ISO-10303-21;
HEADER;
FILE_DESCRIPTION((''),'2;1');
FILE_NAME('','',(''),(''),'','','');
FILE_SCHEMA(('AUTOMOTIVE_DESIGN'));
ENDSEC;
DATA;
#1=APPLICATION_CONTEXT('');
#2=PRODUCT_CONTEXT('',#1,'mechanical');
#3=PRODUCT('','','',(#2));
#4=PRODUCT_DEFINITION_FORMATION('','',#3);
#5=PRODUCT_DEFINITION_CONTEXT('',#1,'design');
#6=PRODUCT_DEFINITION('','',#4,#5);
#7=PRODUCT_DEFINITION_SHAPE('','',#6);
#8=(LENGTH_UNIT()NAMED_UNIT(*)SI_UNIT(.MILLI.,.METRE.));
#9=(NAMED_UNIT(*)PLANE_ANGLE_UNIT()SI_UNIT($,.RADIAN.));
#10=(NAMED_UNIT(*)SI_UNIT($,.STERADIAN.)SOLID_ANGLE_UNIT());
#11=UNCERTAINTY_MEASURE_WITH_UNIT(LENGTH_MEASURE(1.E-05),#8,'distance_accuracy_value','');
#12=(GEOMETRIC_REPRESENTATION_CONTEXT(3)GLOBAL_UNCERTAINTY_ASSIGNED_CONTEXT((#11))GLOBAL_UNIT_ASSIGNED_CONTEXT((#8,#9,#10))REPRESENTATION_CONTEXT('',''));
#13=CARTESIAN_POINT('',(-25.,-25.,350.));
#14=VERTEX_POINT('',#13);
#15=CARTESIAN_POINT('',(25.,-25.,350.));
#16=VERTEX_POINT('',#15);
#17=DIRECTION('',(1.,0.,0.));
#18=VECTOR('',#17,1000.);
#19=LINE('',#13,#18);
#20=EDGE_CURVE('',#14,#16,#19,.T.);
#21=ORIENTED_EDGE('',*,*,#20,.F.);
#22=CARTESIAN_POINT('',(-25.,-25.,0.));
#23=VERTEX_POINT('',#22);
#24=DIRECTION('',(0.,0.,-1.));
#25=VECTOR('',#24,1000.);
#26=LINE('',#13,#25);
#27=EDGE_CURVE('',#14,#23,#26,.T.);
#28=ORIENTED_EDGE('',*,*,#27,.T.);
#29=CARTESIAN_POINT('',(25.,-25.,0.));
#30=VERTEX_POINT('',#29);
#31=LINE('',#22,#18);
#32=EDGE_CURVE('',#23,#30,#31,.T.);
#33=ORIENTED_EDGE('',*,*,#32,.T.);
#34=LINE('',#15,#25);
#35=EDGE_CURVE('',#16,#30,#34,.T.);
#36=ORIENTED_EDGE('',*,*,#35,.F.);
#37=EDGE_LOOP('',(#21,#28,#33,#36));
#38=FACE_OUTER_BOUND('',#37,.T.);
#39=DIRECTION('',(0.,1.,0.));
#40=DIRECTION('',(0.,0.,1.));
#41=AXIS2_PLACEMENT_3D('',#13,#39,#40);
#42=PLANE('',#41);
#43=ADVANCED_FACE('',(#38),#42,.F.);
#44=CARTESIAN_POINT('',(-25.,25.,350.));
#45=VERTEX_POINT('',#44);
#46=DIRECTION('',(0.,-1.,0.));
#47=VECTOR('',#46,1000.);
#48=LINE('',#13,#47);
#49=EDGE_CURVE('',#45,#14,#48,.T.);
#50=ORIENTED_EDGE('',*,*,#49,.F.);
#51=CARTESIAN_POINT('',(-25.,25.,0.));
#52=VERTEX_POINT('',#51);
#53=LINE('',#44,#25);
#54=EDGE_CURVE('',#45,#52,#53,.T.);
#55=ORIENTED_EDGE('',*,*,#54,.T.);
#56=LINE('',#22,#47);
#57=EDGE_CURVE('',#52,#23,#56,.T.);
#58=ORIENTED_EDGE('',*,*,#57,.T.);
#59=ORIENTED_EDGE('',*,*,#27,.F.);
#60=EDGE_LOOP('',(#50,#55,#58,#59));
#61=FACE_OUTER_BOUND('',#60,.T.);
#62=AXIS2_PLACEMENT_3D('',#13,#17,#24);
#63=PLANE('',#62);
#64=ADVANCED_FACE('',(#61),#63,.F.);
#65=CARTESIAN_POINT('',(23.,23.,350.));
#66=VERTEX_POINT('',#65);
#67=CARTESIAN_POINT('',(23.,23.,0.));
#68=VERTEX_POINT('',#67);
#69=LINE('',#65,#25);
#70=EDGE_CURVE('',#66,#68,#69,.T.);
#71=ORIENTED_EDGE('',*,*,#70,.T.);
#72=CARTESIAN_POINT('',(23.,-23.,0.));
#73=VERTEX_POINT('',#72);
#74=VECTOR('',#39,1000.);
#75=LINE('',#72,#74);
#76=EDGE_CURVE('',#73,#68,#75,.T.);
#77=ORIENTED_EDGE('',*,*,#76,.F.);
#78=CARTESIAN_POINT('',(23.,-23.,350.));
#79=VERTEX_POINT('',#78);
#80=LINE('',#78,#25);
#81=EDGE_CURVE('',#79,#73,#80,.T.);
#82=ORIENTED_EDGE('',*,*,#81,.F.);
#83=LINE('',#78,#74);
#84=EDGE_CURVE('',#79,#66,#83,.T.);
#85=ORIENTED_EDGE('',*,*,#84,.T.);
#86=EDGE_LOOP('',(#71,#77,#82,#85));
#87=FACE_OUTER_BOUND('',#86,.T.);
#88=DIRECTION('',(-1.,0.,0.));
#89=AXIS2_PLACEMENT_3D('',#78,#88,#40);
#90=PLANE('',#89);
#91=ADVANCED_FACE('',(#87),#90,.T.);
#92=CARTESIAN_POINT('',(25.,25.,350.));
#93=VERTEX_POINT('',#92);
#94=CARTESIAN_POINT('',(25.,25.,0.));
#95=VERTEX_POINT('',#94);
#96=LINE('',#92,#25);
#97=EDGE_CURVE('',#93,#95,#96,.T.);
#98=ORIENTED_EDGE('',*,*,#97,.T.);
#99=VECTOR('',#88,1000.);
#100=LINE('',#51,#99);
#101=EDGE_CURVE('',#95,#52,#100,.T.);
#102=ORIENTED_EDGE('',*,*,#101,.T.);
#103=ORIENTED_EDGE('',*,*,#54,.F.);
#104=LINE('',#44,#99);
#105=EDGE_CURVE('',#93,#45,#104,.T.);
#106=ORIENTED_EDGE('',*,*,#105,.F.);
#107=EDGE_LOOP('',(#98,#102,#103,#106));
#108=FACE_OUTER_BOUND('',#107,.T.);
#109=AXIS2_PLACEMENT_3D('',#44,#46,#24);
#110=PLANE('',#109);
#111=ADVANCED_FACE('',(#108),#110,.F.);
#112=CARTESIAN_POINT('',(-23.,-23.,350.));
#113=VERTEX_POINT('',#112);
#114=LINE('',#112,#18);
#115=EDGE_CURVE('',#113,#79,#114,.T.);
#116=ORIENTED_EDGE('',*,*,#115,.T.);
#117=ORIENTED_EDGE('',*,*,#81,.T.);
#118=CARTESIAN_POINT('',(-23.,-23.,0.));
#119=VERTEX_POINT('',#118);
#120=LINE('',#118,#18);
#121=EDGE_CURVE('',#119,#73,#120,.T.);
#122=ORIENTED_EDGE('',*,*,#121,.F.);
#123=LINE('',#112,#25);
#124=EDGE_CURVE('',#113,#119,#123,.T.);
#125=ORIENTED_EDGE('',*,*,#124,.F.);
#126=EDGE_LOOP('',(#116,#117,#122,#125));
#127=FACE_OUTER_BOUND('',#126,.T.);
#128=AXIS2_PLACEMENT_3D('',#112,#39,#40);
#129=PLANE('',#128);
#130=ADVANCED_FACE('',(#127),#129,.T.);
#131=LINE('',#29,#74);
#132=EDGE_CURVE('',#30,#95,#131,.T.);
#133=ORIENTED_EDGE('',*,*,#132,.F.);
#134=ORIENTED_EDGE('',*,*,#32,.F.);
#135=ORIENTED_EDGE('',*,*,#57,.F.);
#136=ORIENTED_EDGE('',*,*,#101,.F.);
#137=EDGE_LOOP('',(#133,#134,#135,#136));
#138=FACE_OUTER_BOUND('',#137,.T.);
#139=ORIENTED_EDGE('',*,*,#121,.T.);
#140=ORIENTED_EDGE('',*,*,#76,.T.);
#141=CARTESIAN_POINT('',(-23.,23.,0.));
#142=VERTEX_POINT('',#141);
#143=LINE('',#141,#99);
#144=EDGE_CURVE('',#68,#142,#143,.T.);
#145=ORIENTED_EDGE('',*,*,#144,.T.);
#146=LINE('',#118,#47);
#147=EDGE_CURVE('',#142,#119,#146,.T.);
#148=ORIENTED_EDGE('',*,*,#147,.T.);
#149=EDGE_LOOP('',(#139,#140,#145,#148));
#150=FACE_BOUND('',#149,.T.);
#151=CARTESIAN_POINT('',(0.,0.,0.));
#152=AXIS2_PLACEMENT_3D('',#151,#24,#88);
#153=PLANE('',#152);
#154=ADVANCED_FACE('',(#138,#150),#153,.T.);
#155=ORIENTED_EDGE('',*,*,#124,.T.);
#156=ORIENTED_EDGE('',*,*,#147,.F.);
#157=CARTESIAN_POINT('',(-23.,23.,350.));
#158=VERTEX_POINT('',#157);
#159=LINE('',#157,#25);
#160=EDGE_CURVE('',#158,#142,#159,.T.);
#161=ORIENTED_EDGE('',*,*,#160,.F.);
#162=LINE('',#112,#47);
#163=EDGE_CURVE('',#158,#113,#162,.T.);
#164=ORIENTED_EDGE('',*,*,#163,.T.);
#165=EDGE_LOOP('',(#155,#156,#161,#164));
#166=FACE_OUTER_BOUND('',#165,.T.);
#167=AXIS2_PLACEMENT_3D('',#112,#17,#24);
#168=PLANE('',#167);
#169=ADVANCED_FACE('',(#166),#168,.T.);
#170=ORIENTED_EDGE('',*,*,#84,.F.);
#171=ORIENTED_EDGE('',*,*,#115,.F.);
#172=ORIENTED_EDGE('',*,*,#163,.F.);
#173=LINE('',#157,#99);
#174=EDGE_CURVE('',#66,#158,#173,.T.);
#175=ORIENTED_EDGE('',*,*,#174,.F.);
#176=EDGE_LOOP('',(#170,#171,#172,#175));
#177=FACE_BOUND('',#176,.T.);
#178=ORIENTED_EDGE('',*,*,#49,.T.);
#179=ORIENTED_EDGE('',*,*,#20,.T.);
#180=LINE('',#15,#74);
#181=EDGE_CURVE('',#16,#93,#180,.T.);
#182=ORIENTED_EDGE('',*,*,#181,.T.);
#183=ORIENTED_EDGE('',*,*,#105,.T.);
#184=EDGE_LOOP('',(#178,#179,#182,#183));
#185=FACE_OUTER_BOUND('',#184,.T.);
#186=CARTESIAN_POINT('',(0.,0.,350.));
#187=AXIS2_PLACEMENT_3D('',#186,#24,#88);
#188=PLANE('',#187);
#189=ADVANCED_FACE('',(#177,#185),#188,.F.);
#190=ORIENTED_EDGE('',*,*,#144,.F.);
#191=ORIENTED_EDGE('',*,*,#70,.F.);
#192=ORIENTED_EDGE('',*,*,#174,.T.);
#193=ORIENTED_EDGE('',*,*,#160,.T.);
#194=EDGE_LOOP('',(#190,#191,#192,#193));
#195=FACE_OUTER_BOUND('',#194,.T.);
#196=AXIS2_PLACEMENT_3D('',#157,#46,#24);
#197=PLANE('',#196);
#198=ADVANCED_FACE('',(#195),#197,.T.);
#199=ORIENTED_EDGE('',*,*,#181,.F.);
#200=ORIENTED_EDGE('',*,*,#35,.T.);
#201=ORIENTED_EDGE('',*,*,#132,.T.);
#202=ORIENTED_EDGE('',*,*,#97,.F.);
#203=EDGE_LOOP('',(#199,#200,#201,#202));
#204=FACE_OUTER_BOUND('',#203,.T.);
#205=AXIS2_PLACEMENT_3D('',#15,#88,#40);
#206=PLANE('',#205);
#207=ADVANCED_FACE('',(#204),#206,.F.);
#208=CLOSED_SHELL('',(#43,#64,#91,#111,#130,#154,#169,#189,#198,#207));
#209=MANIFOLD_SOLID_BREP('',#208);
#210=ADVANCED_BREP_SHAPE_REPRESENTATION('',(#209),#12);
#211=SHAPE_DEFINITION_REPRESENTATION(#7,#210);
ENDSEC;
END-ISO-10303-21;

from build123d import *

# Parameters (mm, degrees)
SKETCH1_W           = 50
SKETCH1_H           = 50
SKETCH1_W_2         = 46
SKETCH1_H_2         = 46
BOSS_EXTRUDE1_DEPTH = 350


with BuildPart() as part:
    # Sketch1 → Boss-Extrude1 (new body)
    with BuildSketch(Plane.XY):
        Rectangle(SKETCH1_W, SKETCH1_H)
        Rectangle(SKETCH1_W_2, SKETCH1_H_2, mode=Mode.SUBTRACT)
    extrude(amount=BOSS_EXTRUDE1_DEPTH)


solid = part.part
